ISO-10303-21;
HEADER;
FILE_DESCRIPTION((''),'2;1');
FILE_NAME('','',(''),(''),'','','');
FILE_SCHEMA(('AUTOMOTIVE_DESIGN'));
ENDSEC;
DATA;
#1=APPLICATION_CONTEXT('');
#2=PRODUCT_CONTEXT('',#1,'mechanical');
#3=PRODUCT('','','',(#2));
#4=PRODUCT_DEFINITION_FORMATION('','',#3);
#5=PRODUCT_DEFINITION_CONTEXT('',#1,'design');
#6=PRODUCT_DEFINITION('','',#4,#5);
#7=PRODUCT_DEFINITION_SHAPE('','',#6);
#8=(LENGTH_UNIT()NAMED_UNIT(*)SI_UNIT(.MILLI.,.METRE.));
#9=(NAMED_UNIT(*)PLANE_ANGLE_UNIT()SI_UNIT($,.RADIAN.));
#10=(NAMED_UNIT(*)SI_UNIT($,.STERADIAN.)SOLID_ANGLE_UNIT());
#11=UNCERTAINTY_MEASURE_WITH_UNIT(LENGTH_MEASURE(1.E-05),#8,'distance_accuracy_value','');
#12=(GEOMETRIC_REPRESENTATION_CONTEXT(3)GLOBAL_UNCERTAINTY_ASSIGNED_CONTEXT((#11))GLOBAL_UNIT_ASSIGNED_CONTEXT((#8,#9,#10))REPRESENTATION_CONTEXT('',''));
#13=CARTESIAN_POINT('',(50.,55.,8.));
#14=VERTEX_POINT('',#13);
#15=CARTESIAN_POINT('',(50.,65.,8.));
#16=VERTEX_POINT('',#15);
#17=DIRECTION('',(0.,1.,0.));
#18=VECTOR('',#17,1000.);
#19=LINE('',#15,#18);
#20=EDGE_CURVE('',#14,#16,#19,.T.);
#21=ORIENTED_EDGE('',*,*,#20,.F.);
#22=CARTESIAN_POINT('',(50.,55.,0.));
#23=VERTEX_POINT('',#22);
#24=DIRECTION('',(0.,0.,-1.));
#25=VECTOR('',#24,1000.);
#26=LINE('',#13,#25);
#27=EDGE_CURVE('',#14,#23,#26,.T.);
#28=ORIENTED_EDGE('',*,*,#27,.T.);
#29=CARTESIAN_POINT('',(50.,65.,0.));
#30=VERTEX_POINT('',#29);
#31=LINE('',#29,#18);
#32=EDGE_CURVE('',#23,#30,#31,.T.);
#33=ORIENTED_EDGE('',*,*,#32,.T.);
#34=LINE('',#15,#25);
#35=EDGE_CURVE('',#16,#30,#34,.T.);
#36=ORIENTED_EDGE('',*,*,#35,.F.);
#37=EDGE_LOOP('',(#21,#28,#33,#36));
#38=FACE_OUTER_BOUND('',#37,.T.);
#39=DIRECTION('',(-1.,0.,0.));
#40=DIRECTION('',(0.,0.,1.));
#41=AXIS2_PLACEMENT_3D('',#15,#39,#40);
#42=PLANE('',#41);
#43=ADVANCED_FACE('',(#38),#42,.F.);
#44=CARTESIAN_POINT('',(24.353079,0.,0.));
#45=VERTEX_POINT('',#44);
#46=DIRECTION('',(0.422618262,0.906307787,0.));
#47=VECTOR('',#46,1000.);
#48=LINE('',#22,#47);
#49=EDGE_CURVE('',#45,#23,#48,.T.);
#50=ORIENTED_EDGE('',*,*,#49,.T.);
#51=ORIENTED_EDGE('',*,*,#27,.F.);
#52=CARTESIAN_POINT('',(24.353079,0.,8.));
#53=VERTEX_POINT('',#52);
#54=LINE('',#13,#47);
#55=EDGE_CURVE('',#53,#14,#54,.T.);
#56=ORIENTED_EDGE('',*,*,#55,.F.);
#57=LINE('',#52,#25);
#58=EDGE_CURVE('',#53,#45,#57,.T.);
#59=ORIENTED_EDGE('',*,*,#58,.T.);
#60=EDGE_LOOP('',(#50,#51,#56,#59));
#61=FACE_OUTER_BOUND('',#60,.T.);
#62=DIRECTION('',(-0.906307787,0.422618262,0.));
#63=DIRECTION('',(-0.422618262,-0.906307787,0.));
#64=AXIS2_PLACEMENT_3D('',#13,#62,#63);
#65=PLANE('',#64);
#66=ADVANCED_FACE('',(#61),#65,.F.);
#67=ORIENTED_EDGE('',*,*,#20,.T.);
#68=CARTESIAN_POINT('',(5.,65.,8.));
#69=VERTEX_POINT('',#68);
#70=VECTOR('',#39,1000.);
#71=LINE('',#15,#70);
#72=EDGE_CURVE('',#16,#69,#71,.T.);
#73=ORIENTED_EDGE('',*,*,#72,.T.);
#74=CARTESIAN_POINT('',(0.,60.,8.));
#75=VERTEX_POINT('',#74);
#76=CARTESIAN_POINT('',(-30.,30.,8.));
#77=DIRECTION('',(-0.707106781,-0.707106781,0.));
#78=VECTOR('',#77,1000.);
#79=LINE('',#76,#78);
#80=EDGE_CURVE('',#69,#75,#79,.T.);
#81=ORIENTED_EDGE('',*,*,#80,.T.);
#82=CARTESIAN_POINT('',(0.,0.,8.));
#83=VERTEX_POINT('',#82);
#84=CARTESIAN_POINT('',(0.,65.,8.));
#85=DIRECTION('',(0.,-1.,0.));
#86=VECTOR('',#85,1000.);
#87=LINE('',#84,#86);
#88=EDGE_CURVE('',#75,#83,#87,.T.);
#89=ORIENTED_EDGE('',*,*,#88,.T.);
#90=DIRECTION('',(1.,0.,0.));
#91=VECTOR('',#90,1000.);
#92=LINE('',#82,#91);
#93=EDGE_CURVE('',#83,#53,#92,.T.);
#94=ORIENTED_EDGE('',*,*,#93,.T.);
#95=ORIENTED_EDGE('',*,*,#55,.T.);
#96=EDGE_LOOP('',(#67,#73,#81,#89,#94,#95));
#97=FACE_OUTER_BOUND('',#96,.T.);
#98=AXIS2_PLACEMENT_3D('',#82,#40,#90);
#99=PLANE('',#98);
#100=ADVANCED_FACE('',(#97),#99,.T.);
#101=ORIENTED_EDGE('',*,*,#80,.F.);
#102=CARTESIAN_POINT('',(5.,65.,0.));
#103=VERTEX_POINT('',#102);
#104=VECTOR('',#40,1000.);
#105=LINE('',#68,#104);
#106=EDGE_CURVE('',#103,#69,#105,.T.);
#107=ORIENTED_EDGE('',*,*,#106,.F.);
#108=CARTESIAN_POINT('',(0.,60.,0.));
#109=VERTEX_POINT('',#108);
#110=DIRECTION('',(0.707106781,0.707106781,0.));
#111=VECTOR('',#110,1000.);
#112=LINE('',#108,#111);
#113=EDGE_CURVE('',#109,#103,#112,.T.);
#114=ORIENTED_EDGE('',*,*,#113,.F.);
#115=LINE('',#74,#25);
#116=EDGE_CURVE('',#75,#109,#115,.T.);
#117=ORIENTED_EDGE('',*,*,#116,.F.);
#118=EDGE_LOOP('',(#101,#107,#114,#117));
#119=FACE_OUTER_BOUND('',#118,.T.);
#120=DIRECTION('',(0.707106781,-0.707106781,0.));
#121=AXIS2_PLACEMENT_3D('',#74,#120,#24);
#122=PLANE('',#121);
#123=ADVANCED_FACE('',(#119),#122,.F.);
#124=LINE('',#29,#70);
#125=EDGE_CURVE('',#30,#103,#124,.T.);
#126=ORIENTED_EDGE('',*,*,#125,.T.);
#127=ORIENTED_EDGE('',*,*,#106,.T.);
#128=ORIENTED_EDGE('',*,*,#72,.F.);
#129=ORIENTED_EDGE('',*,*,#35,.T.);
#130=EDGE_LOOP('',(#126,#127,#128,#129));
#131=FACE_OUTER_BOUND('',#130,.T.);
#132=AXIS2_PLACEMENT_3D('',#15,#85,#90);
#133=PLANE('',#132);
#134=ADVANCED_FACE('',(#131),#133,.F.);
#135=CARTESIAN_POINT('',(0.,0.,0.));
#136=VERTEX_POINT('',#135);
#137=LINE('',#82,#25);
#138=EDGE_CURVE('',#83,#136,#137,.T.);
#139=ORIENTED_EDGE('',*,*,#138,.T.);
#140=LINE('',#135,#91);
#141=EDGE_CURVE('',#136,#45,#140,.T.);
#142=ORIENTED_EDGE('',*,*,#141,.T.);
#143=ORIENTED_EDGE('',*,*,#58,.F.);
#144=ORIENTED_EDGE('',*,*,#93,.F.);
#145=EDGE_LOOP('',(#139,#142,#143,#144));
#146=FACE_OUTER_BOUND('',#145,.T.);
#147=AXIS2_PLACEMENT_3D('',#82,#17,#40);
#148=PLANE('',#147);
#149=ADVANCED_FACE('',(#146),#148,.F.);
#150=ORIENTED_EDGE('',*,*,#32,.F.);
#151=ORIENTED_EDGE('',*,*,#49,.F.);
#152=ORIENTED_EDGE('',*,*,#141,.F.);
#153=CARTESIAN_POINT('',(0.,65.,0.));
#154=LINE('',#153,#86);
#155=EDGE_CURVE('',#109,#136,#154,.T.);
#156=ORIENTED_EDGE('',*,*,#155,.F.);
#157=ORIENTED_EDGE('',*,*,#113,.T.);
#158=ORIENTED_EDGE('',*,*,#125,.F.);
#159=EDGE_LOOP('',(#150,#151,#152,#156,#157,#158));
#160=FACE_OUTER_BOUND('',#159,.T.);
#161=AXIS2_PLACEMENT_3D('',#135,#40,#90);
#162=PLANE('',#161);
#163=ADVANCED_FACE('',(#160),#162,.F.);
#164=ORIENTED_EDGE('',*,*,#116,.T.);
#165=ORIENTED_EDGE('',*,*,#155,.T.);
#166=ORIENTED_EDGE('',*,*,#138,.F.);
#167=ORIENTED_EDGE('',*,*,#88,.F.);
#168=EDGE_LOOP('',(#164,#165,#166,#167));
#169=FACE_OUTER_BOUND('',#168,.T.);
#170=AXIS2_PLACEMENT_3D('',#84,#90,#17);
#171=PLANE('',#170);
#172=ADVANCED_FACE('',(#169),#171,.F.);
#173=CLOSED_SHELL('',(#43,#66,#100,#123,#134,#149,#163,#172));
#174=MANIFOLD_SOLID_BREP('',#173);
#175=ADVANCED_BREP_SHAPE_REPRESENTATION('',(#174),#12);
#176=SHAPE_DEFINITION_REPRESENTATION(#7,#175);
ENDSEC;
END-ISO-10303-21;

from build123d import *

# Parameters (mm, degrees)
BOSS_EXTRUDE1_DEPTH = 8
CHAMFER1_SIZE       = 5


with BuildPart() as part:
    # Sketch1 → Boss-Extrude1 (new body)
    with BuildSketch(Plane.XY):
        Polygon((50, 65), (0, 65), (0, 0), (24.353078801, 0), (50, 55), align=None)
    extrude(amount=BOSS_EXTRUDE1_DEPTH)

    # Chamfer1
    chamfer1_edges = [part.edges().sort_by_distance(p)[0] for p in [
        (0, 65, 4),
    ]]
    chamfer(chamfer1_edges, length=CHAMFER1_SIZE)


solid = part.part
